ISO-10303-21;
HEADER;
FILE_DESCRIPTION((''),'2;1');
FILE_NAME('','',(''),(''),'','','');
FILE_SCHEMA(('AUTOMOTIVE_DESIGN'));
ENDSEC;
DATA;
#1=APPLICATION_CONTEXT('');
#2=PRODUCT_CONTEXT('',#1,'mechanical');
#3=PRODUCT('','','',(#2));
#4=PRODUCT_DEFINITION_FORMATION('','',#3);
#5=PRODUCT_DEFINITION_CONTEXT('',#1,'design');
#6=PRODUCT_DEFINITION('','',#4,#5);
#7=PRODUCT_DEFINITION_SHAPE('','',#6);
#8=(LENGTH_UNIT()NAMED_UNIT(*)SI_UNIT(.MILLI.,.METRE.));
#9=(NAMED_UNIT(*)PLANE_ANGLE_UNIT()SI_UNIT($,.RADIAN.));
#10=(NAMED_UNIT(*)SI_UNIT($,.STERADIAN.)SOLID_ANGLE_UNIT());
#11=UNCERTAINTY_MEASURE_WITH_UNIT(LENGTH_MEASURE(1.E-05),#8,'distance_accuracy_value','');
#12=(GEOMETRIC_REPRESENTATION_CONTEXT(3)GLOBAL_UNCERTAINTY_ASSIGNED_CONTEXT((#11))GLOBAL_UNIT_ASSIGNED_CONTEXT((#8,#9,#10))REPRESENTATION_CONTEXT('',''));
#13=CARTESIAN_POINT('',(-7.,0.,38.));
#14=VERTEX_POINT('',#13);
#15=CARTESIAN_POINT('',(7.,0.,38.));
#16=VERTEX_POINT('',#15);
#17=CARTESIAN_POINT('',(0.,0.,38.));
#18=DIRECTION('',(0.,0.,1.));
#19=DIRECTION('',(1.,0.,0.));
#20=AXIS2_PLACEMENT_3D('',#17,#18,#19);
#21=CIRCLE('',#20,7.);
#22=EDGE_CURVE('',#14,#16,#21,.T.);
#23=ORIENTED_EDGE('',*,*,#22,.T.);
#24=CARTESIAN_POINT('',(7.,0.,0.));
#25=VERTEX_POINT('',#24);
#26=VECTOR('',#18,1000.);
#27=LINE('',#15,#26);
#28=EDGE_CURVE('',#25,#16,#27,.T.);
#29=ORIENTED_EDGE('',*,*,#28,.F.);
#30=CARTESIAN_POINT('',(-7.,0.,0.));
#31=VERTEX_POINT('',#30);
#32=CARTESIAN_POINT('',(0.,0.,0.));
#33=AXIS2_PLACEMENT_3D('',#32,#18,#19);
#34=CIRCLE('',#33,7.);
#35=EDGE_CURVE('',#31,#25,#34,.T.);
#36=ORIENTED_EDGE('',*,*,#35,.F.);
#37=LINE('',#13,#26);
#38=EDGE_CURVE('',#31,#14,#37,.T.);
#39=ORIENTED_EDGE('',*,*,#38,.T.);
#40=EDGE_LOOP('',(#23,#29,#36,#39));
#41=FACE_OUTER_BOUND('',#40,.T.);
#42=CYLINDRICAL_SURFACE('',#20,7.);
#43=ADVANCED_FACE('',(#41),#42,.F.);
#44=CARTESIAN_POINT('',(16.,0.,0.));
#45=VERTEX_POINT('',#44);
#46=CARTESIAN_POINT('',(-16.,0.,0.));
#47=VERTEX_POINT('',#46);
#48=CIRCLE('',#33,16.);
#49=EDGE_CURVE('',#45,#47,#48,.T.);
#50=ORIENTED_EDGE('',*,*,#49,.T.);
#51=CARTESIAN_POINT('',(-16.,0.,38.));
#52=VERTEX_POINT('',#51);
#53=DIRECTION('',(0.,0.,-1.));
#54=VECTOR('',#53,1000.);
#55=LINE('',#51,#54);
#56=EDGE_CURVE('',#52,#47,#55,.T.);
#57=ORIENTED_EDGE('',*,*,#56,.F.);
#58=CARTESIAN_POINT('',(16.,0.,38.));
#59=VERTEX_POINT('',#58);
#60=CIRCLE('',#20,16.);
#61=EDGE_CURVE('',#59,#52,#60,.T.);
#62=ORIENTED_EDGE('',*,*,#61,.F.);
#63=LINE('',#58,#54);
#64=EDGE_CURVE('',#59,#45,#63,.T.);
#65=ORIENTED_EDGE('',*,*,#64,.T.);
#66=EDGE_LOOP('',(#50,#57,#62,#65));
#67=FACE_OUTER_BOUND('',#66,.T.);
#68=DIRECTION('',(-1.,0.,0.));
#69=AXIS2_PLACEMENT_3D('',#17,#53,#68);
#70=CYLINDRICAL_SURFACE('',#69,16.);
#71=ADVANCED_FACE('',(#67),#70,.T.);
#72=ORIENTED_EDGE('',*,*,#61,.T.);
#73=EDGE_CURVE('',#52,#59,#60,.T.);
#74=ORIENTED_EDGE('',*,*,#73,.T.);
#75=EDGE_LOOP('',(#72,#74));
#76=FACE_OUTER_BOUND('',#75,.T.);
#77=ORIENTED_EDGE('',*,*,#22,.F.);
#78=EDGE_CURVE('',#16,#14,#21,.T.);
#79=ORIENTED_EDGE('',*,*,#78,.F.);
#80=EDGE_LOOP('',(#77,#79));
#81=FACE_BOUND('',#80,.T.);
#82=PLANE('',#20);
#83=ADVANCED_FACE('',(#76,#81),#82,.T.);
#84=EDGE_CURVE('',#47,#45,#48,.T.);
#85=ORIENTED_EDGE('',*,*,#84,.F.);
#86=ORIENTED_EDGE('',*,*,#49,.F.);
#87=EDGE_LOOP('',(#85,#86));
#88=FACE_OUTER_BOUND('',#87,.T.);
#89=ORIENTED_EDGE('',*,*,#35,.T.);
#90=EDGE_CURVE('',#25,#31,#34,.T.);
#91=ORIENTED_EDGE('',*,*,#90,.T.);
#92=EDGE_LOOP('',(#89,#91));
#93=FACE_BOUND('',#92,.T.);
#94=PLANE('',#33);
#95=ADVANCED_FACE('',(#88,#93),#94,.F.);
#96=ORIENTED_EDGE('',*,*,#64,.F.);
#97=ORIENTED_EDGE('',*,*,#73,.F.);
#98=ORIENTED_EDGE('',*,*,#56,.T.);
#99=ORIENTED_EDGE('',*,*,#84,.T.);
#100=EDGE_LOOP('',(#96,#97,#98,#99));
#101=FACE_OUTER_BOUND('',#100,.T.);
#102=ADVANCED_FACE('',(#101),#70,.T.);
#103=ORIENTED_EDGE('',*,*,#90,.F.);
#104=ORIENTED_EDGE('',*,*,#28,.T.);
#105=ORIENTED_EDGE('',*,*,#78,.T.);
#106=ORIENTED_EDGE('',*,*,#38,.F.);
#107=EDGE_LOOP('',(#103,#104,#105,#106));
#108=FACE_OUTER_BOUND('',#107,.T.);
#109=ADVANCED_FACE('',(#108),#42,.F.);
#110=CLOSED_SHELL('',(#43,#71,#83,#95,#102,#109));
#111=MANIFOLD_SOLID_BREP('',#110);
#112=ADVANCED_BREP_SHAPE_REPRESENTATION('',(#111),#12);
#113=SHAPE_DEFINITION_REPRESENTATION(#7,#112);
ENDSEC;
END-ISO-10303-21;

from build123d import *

# Parameters (mm, degrees)
SKETCH1_R           = 16
BOSS_EXTRUDE1_DEPTH = 38
M16_TAPPED_HOLE1_D  = 14


with BuildPart() as part:
    # Sketch1 → Boss-Extrude1 (new body)
    with BuildSketch(Plane.XY):
        Circle(SKETCH1_R)
    extrude(amount=BOSS_EXTRUDE1_DEPTH)

    # M16 Tapped Hole1 (through all)
    with Locations(Plane.XY.offset(38)):
        with Locations((0, 0)):
            Hole(M16_TAPPED_HOLE1_D / 2)


solid = part.part
